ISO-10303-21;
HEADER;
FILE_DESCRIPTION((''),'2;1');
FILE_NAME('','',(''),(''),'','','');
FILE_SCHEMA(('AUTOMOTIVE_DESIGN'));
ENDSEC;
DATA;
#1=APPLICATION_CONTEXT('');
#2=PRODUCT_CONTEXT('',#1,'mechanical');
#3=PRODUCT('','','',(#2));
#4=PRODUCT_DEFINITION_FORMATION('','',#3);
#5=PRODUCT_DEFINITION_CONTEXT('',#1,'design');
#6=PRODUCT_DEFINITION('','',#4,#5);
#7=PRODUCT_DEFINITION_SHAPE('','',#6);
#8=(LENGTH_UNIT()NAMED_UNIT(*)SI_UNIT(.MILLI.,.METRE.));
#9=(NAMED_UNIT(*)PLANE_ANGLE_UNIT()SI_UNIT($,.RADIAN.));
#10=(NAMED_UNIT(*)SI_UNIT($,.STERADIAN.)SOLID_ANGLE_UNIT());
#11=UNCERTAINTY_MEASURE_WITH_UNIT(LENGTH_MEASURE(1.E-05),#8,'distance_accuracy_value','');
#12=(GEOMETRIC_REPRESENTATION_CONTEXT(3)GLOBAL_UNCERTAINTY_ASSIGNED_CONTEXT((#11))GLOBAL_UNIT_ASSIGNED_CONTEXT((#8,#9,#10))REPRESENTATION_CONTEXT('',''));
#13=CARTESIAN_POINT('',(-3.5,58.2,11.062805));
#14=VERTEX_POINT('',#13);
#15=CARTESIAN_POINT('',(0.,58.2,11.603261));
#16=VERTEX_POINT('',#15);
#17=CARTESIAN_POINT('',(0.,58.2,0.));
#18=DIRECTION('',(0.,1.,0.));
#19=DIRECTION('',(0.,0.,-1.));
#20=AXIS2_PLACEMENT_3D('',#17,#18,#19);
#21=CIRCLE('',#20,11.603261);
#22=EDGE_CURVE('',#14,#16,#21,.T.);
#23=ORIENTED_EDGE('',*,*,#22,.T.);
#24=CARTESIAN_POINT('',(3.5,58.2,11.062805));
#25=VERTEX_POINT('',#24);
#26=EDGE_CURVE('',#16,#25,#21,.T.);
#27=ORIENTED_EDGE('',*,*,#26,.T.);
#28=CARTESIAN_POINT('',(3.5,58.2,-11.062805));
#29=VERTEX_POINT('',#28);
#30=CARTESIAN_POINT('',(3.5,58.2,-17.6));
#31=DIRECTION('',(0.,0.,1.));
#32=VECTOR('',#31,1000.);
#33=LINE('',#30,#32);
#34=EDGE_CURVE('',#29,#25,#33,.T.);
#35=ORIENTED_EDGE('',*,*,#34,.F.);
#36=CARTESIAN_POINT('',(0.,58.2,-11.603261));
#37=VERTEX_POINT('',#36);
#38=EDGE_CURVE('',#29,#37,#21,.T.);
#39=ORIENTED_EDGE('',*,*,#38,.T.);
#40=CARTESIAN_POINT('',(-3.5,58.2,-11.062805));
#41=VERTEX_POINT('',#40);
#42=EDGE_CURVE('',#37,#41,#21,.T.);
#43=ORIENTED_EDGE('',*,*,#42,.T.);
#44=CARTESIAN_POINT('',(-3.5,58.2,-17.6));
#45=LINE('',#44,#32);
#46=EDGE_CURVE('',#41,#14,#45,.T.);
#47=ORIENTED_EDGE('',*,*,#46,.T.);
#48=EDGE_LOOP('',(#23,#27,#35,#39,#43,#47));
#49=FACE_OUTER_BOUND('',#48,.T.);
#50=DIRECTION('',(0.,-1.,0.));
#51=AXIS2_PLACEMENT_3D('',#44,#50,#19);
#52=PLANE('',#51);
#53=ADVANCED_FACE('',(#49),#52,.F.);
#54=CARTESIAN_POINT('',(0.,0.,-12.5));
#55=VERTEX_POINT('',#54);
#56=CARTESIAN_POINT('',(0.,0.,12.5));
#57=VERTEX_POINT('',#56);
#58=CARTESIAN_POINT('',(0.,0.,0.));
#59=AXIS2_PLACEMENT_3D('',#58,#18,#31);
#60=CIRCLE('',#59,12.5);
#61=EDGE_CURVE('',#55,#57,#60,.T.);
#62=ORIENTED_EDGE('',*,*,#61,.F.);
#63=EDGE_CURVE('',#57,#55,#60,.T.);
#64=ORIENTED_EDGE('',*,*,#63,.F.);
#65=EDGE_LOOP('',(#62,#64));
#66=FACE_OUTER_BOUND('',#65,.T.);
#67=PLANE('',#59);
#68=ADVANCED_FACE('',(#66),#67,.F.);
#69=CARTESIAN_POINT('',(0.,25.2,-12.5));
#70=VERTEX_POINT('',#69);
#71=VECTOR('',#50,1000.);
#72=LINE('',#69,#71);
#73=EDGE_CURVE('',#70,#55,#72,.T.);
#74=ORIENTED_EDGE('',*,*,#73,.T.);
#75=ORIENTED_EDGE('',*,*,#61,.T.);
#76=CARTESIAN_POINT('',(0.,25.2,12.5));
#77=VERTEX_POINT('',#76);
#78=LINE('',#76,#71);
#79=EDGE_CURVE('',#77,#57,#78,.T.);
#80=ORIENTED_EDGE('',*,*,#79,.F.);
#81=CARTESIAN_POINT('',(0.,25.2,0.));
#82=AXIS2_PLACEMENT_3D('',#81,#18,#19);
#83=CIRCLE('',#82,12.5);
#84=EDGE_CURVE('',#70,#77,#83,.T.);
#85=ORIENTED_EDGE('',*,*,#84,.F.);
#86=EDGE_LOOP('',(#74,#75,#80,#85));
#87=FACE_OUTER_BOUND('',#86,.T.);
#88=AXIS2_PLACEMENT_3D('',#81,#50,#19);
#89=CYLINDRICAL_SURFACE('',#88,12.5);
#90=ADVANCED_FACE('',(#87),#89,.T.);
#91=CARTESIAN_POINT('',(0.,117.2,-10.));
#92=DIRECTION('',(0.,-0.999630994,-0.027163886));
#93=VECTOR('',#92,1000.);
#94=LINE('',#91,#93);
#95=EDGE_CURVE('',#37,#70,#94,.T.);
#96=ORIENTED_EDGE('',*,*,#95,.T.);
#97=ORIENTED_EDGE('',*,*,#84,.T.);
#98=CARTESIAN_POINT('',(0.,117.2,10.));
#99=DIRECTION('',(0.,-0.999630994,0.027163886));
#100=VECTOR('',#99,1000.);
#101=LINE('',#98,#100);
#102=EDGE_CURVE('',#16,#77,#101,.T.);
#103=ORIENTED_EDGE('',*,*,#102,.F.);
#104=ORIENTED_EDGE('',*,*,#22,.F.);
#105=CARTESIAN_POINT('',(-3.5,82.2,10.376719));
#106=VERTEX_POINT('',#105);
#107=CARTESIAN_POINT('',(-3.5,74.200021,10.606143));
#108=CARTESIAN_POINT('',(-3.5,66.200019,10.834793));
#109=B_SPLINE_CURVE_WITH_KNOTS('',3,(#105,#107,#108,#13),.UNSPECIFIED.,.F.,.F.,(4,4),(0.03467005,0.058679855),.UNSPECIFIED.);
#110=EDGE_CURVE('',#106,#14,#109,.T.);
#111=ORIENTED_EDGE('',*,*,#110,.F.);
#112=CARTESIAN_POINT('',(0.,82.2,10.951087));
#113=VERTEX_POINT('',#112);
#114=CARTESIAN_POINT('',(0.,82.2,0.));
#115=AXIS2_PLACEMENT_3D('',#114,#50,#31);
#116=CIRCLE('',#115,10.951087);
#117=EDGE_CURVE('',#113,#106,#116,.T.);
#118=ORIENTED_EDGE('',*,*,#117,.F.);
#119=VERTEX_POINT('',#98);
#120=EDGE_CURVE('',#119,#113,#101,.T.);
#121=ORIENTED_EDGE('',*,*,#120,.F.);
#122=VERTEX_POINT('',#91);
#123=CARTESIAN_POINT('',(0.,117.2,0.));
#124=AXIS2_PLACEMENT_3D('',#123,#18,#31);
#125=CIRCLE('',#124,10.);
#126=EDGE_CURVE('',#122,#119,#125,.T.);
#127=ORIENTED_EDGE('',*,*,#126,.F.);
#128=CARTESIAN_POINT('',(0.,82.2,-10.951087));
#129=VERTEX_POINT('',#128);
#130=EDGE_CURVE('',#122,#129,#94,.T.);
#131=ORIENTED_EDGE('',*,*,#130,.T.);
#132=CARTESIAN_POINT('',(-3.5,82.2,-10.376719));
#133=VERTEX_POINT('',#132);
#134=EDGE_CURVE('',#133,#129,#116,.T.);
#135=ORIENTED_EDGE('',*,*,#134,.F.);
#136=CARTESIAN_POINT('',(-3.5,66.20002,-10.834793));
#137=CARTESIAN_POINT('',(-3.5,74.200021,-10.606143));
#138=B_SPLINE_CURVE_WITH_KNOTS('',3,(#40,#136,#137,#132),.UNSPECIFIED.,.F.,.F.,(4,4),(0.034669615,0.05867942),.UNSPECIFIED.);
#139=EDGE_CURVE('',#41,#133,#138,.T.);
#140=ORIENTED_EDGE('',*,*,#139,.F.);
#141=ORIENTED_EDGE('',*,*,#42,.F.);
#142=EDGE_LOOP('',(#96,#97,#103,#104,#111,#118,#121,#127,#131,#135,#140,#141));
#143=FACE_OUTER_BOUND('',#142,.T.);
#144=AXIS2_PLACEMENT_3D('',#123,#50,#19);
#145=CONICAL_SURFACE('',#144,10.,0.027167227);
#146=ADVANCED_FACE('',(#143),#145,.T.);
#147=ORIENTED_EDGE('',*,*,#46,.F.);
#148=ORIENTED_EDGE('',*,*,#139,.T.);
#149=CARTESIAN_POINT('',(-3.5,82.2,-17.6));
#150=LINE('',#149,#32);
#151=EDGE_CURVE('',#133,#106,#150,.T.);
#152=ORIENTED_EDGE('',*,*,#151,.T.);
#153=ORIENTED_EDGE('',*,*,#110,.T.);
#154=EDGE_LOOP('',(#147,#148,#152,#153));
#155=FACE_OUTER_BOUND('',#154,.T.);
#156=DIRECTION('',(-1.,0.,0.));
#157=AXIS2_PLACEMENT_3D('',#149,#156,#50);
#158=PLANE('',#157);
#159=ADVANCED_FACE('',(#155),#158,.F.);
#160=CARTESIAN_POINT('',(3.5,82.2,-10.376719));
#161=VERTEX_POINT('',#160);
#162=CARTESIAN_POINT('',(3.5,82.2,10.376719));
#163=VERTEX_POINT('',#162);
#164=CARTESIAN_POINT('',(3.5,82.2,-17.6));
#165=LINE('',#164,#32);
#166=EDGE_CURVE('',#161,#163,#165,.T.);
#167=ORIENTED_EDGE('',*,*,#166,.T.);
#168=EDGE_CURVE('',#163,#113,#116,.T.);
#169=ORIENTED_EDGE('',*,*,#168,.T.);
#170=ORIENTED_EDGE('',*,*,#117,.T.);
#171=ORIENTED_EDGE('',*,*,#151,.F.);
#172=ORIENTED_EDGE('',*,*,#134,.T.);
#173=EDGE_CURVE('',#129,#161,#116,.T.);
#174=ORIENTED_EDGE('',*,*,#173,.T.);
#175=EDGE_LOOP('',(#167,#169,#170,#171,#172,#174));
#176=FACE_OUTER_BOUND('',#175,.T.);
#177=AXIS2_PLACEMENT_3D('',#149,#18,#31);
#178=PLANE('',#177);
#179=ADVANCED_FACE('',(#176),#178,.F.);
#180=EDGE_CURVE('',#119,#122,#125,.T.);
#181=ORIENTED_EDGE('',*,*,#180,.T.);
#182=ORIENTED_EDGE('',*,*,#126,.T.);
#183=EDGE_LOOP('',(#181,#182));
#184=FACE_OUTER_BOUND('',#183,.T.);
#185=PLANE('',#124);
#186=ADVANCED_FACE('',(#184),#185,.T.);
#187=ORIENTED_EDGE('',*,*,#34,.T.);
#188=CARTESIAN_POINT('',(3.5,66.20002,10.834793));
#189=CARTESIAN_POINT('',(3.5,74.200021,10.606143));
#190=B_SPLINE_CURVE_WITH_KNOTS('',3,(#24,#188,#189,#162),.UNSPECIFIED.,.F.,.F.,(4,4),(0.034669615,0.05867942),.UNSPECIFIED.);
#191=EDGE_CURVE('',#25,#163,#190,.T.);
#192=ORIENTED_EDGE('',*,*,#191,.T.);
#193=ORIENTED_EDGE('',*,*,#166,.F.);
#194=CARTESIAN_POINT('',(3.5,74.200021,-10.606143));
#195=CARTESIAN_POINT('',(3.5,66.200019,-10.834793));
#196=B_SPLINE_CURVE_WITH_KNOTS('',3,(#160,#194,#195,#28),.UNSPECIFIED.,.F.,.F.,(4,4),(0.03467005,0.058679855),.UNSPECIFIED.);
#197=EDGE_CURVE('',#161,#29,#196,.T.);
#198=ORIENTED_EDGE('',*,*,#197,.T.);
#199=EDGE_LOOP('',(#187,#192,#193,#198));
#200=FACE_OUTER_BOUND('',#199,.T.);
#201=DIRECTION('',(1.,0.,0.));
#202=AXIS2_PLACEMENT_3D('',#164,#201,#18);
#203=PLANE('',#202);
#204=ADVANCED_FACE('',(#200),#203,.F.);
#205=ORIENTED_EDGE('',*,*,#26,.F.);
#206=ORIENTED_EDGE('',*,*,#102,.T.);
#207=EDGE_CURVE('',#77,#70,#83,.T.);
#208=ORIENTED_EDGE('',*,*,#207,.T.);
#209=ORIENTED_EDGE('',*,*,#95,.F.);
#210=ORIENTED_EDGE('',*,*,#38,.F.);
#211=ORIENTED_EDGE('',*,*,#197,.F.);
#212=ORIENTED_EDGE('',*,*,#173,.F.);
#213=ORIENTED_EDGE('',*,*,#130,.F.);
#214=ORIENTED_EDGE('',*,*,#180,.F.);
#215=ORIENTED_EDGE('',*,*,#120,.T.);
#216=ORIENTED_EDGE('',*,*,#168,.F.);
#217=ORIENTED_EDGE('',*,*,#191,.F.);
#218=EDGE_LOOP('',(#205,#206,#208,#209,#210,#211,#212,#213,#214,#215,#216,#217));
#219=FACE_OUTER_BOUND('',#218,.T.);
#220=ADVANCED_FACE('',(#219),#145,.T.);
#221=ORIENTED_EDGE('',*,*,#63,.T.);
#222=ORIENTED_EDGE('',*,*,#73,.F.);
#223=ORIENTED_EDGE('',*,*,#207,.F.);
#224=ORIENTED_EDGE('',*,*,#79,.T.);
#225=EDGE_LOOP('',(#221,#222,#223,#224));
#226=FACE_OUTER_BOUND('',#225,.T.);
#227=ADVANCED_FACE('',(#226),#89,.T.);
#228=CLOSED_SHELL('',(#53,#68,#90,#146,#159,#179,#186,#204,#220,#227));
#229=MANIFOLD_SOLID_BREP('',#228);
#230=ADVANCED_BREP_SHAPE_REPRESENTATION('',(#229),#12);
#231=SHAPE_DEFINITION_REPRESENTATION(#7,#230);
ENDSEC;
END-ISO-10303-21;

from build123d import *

# Parameters (mm, degrees)
BASE_SHANK_PROFILE_25_2_R  = 12.5
BASE_SHANK_25_2_DEPTH      = 25.2
TAPER_START_PROFILE_25_2_R = 12.5
TAPER_END_PROFILE_20_2_R   = 10
THROUGH_SLOT_PROFILE_W     = 7
THROUGH_SLOT_PROFILE_H     = 24
THROUGH_SLOT_DEPTH         = 17.6


with BuildPart() as part:
    # Base Shank Profile Ø25.2 → Base Shank Ø25.2 (new body)
    with BuildSketch(Plane(origin=(0, 0, 0), x_dir=(1, 0, 0), z_dir=(0, 1, 0))):
        with Locations(Location((0, 0, 0), (0, 0, 270))):
            Circle(BASE_SHANK_PROFILE_25_2_R)
    extrude(amount=BASE_SHANK_25_2_DEPTH)

    # Taper Start Profile Ø25.2 → Tapered Rod Loft section 0
    with BuildSketch(Plane(origin=(0, 25.2, 0), x_dir=(1, 0, 0), z_dir=(0, 1, 0))):
        Circle(TAPER_START_PROFILE_25_2_R)
    # Taper End Profile Ø20.2 → Tapered Rod Loft section 1
    with BuildSketch(Plane(origin=(0, 117.2, 0), x_dir=(1, 0, 0), z_dir=(0, 1, 0))):
        Circle(TAPER_END_PROFILE_20_2_R)
    loft()

    # Through Slot Profile → Through Slot (cut, symmetric)
    with BuildSketch(Plane.XY):
        with Locations((0, 70.2)):
            Rectangle(THROUGH_SLOT_PROFILE_W, THROUGH_SLOT_PROFILE_H)
    extrude(amount=THROUGH_SLOT_DEPTH, both=True, mode=Mode.SUBTRACT)


solid = part.part
